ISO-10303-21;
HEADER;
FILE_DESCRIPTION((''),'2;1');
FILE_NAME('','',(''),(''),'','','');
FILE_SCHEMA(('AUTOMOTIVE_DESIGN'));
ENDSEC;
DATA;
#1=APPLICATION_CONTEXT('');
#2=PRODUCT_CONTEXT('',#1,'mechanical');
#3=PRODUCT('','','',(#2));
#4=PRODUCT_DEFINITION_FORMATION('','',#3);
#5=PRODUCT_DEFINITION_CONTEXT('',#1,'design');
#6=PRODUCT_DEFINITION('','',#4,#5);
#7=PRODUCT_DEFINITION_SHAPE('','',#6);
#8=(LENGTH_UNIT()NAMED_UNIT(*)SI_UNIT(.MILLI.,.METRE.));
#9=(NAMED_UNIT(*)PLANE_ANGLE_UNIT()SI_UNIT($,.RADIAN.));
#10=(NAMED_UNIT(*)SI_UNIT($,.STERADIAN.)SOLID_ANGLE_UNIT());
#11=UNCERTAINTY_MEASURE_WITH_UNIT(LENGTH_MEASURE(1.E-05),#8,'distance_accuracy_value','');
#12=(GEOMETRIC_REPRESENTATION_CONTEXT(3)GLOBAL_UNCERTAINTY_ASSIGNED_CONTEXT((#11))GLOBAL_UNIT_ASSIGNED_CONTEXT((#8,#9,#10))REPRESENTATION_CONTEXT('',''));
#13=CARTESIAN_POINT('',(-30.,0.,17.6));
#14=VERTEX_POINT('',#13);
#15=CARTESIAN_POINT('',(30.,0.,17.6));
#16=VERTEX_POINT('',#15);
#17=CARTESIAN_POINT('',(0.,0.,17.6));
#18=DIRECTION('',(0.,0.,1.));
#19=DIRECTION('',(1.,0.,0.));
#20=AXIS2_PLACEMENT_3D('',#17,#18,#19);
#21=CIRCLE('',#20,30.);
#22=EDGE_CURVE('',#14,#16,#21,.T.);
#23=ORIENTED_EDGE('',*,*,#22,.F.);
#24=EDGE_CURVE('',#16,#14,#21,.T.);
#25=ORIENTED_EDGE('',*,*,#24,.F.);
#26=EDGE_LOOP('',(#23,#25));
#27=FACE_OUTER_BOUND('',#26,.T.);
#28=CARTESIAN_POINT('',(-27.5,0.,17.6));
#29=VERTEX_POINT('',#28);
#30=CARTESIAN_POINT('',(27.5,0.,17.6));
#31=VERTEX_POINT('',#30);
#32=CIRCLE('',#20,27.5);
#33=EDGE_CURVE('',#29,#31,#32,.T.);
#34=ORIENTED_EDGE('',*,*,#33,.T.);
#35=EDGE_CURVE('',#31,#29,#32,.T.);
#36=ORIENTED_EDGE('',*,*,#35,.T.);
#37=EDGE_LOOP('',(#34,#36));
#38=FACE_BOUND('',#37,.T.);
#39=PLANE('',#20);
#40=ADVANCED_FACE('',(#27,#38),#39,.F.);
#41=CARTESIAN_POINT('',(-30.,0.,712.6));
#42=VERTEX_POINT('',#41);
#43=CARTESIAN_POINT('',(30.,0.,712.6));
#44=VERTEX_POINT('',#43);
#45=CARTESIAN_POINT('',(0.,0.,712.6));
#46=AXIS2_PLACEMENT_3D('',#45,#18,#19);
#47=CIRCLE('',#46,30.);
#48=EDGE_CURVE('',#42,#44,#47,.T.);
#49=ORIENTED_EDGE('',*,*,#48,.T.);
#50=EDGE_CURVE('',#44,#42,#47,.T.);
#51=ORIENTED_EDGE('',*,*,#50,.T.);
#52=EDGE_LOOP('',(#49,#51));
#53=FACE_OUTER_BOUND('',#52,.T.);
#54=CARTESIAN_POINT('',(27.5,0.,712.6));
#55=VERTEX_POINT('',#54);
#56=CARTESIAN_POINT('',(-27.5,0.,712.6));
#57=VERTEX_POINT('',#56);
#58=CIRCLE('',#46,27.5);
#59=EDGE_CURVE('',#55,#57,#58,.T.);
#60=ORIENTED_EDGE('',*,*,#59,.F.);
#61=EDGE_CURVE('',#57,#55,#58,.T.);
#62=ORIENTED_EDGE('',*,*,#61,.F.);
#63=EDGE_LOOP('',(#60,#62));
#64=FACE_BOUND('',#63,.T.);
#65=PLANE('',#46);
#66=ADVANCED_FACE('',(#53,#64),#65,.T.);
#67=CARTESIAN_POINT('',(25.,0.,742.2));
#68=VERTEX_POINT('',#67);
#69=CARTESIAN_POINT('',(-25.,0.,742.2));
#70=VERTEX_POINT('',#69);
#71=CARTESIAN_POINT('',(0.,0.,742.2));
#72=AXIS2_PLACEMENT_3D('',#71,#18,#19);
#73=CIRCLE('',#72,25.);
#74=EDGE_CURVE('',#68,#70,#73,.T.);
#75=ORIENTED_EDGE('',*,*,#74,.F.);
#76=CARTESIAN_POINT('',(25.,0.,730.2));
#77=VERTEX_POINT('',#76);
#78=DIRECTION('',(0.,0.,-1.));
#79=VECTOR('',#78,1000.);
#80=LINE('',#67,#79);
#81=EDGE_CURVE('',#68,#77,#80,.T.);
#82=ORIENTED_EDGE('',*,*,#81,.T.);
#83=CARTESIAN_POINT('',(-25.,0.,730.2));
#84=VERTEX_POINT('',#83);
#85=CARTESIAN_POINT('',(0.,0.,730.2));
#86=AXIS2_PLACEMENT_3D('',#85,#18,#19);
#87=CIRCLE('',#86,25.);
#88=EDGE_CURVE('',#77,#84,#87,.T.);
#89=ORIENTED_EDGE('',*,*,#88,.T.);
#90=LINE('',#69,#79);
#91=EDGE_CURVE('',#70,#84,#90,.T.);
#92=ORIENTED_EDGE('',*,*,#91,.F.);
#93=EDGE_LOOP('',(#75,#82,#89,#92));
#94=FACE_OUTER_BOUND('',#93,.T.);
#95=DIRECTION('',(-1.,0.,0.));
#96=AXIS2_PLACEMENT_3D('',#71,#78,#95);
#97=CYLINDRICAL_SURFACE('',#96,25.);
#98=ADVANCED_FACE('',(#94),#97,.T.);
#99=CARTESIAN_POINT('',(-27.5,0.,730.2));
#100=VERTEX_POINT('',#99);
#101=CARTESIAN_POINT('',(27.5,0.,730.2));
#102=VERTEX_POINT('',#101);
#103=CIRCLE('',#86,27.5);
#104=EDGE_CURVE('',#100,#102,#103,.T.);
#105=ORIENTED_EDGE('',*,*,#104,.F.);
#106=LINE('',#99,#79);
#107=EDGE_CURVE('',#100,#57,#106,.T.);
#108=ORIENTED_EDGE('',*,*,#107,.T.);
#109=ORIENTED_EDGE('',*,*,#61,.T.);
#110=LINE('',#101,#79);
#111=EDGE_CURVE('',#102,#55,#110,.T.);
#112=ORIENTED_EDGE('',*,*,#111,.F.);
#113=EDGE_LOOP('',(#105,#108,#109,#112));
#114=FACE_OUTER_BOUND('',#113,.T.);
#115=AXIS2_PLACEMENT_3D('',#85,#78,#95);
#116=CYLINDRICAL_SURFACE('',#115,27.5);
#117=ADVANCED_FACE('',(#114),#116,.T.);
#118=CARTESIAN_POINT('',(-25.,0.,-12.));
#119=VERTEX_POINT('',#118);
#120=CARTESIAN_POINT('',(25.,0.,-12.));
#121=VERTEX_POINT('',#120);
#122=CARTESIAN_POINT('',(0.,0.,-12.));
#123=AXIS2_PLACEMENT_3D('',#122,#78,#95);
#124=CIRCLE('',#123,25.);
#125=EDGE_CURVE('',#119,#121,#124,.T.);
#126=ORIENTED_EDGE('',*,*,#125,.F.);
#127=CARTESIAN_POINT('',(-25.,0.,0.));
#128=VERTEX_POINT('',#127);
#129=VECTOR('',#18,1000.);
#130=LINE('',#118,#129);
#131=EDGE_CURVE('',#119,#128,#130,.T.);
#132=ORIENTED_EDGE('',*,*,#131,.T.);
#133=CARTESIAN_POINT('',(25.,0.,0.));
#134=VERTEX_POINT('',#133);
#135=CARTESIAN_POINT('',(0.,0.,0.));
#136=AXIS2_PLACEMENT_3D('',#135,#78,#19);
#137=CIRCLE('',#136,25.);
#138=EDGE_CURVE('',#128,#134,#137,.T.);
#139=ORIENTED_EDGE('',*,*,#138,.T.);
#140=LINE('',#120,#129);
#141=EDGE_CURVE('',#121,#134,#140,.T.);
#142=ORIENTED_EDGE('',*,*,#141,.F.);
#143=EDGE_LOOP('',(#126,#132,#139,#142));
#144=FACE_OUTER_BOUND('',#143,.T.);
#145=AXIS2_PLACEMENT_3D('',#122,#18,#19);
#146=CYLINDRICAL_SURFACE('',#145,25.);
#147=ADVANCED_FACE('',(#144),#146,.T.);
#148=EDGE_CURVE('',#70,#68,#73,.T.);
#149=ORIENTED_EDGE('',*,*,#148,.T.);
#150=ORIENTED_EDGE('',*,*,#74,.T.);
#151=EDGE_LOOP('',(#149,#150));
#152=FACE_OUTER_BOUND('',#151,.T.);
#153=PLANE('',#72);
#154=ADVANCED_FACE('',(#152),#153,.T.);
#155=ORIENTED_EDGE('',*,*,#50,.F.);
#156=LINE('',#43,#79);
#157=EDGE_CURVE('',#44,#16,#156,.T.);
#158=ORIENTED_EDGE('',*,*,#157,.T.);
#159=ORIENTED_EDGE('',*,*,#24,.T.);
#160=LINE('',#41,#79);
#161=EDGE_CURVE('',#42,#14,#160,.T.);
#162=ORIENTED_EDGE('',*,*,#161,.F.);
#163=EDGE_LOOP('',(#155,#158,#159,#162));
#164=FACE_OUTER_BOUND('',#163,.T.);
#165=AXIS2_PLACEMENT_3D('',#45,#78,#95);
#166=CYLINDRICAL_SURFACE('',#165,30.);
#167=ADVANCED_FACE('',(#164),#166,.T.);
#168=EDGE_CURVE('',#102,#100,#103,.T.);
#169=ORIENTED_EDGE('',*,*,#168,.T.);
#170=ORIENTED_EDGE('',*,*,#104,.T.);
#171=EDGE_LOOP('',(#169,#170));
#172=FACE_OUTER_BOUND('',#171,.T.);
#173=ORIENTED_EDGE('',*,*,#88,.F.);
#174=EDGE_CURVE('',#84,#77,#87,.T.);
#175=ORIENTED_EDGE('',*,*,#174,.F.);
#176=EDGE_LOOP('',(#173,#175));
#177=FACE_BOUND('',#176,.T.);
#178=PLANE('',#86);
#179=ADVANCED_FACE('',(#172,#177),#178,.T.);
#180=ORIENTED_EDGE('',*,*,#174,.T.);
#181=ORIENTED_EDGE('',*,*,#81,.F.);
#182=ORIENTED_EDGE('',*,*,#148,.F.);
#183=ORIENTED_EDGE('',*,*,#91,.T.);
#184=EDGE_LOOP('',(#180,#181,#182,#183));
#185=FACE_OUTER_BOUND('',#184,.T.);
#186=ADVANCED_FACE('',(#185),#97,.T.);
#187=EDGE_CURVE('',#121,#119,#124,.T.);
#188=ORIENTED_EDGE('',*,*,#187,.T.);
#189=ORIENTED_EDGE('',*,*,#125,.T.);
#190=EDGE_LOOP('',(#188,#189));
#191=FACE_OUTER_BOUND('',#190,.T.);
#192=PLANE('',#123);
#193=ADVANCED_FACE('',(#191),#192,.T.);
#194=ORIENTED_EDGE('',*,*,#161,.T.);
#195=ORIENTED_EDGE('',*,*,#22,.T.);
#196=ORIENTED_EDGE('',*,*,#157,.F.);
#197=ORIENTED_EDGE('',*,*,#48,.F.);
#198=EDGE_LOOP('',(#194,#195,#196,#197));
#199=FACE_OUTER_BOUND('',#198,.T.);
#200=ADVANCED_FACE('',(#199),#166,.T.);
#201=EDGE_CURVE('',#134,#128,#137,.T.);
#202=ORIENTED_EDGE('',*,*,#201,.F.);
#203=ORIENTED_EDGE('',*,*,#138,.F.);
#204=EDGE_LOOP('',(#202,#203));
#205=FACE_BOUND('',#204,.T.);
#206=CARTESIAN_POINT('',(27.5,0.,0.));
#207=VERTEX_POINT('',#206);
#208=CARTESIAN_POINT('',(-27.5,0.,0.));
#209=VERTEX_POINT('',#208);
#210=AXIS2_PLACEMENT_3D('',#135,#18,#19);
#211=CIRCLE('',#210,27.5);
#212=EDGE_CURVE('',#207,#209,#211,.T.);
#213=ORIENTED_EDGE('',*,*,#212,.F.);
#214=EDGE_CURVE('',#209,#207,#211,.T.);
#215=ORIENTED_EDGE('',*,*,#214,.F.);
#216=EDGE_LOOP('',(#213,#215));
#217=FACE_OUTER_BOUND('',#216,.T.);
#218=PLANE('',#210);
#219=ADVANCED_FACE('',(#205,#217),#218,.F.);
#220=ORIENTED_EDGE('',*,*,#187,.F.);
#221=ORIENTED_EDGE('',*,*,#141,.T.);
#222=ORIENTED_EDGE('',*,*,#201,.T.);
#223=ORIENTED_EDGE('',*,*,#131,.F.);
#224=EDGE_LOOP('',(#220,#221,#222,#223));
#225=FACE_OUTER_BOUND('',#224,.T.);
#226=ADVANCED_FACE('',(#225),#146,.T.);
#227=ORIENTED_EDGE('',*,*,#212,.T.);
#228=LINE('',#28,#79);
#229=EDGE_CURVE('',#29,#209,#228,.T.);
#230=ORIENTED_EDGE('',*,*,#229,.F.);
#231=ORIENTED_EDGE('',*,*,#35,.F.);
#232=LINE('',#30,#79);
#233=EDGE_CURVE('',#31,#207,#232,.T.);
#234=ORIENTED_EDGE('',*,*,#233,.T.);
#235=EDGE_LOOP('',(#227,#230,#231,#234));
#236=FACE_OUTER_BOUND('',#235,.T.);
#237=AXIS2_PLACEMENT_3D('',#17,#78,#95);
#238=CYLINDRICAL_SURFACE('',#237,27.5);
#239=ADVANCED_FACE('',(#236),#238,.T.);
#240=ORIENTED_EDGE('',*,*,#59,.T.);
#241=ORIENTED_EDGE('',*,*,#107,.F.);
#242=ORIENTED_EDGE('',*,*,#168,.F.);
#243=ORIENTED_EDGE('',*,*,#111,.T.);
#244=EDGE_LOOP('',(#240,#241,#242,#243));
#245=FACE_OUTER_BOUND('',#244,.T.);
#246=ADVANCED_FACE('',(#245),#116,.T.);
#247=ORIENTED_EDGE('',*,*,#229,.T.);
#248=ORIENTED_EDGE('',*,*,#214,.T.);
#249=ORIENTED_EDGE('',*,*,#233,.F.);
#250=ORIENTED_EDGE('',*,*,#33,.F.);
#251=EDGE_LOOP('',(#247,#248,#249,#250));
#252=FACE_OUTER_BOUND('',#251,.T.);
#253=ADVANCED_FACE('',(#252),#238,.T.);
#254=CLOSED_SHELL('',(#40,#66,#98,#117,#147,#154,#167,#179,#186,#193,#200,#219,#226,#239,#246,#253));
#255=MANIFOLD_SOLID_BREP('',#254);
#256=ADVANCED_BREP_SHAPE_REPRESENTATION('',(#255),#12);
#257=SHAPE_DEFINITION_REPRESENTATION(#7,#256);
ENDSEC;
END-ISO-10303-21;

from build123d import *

# Parameters (mm, degrees)
SKETCH1_R           = 27.5
BOSS_EXTRUDE1_DEPTH = 17.6
SKETCH2_R           = 25
BOSS_EXTRUDE2_DEPTH = 12
SKETCH3_R           = 30
BOSS_EXTRUDE3_DEPTH = 695
SKETCH4_R           = 27.5
BOSS_EXTRUDE4_DEPTH = 17.6
BOSS_EXTRUDE5_START = 12
SKETCH5_R           = 25
BOSS_EXTRUDE5_DEPTH = 12


with BuildPart() as part:
    # Sketch1 → Boss-Extrude1 (new body)
    with BuildSketch(Plane.XY):
        Circle(SKETCH1_R)
    extrude(amount=BOSS_EXTRUDE1_DEPTH)

    # Sketch2 → Boss-Extrude2 (add)
    with BuildSketch(Plane(origin=(0, 0, 0), x_dir=(-1, 0, 0), z_dir=(0, 0, -1))):
        with Locations(Location((0, 0, 0), (0, 0, 180))):
            Circle(SKETCH2_R)
    extrude(amount=BOSS_EXTRUDE2_DEPTH)

    # Sketch3 → Boss-Extrude3 (add)
    with BuildSketch(Plane.XY.offset(17.6)):
        Circle(SKETCH3_R)
    extrude(amount=BOSS_EXTRUDE3_DEPTH)

    # Sketch4 → Boss-Extrude4 (add)
    with BuildSketch(Plane.XY.offset(712.6)):
        Circle(SKETCH4_R)
    extrude(amount=BOSS_EXTRUDE4_DEPTH)

    # Sketch5 → Boss-Extrude5 (add)
    with BuildSketch(Plane.XY.offset(730.2).offset(BOSS_EXTRUDE5_START)):
        Circle(SKETCH5_R)
    extrude(amount=-BOSS_EXTRUDE5_DEPTH)


solid = part.part
